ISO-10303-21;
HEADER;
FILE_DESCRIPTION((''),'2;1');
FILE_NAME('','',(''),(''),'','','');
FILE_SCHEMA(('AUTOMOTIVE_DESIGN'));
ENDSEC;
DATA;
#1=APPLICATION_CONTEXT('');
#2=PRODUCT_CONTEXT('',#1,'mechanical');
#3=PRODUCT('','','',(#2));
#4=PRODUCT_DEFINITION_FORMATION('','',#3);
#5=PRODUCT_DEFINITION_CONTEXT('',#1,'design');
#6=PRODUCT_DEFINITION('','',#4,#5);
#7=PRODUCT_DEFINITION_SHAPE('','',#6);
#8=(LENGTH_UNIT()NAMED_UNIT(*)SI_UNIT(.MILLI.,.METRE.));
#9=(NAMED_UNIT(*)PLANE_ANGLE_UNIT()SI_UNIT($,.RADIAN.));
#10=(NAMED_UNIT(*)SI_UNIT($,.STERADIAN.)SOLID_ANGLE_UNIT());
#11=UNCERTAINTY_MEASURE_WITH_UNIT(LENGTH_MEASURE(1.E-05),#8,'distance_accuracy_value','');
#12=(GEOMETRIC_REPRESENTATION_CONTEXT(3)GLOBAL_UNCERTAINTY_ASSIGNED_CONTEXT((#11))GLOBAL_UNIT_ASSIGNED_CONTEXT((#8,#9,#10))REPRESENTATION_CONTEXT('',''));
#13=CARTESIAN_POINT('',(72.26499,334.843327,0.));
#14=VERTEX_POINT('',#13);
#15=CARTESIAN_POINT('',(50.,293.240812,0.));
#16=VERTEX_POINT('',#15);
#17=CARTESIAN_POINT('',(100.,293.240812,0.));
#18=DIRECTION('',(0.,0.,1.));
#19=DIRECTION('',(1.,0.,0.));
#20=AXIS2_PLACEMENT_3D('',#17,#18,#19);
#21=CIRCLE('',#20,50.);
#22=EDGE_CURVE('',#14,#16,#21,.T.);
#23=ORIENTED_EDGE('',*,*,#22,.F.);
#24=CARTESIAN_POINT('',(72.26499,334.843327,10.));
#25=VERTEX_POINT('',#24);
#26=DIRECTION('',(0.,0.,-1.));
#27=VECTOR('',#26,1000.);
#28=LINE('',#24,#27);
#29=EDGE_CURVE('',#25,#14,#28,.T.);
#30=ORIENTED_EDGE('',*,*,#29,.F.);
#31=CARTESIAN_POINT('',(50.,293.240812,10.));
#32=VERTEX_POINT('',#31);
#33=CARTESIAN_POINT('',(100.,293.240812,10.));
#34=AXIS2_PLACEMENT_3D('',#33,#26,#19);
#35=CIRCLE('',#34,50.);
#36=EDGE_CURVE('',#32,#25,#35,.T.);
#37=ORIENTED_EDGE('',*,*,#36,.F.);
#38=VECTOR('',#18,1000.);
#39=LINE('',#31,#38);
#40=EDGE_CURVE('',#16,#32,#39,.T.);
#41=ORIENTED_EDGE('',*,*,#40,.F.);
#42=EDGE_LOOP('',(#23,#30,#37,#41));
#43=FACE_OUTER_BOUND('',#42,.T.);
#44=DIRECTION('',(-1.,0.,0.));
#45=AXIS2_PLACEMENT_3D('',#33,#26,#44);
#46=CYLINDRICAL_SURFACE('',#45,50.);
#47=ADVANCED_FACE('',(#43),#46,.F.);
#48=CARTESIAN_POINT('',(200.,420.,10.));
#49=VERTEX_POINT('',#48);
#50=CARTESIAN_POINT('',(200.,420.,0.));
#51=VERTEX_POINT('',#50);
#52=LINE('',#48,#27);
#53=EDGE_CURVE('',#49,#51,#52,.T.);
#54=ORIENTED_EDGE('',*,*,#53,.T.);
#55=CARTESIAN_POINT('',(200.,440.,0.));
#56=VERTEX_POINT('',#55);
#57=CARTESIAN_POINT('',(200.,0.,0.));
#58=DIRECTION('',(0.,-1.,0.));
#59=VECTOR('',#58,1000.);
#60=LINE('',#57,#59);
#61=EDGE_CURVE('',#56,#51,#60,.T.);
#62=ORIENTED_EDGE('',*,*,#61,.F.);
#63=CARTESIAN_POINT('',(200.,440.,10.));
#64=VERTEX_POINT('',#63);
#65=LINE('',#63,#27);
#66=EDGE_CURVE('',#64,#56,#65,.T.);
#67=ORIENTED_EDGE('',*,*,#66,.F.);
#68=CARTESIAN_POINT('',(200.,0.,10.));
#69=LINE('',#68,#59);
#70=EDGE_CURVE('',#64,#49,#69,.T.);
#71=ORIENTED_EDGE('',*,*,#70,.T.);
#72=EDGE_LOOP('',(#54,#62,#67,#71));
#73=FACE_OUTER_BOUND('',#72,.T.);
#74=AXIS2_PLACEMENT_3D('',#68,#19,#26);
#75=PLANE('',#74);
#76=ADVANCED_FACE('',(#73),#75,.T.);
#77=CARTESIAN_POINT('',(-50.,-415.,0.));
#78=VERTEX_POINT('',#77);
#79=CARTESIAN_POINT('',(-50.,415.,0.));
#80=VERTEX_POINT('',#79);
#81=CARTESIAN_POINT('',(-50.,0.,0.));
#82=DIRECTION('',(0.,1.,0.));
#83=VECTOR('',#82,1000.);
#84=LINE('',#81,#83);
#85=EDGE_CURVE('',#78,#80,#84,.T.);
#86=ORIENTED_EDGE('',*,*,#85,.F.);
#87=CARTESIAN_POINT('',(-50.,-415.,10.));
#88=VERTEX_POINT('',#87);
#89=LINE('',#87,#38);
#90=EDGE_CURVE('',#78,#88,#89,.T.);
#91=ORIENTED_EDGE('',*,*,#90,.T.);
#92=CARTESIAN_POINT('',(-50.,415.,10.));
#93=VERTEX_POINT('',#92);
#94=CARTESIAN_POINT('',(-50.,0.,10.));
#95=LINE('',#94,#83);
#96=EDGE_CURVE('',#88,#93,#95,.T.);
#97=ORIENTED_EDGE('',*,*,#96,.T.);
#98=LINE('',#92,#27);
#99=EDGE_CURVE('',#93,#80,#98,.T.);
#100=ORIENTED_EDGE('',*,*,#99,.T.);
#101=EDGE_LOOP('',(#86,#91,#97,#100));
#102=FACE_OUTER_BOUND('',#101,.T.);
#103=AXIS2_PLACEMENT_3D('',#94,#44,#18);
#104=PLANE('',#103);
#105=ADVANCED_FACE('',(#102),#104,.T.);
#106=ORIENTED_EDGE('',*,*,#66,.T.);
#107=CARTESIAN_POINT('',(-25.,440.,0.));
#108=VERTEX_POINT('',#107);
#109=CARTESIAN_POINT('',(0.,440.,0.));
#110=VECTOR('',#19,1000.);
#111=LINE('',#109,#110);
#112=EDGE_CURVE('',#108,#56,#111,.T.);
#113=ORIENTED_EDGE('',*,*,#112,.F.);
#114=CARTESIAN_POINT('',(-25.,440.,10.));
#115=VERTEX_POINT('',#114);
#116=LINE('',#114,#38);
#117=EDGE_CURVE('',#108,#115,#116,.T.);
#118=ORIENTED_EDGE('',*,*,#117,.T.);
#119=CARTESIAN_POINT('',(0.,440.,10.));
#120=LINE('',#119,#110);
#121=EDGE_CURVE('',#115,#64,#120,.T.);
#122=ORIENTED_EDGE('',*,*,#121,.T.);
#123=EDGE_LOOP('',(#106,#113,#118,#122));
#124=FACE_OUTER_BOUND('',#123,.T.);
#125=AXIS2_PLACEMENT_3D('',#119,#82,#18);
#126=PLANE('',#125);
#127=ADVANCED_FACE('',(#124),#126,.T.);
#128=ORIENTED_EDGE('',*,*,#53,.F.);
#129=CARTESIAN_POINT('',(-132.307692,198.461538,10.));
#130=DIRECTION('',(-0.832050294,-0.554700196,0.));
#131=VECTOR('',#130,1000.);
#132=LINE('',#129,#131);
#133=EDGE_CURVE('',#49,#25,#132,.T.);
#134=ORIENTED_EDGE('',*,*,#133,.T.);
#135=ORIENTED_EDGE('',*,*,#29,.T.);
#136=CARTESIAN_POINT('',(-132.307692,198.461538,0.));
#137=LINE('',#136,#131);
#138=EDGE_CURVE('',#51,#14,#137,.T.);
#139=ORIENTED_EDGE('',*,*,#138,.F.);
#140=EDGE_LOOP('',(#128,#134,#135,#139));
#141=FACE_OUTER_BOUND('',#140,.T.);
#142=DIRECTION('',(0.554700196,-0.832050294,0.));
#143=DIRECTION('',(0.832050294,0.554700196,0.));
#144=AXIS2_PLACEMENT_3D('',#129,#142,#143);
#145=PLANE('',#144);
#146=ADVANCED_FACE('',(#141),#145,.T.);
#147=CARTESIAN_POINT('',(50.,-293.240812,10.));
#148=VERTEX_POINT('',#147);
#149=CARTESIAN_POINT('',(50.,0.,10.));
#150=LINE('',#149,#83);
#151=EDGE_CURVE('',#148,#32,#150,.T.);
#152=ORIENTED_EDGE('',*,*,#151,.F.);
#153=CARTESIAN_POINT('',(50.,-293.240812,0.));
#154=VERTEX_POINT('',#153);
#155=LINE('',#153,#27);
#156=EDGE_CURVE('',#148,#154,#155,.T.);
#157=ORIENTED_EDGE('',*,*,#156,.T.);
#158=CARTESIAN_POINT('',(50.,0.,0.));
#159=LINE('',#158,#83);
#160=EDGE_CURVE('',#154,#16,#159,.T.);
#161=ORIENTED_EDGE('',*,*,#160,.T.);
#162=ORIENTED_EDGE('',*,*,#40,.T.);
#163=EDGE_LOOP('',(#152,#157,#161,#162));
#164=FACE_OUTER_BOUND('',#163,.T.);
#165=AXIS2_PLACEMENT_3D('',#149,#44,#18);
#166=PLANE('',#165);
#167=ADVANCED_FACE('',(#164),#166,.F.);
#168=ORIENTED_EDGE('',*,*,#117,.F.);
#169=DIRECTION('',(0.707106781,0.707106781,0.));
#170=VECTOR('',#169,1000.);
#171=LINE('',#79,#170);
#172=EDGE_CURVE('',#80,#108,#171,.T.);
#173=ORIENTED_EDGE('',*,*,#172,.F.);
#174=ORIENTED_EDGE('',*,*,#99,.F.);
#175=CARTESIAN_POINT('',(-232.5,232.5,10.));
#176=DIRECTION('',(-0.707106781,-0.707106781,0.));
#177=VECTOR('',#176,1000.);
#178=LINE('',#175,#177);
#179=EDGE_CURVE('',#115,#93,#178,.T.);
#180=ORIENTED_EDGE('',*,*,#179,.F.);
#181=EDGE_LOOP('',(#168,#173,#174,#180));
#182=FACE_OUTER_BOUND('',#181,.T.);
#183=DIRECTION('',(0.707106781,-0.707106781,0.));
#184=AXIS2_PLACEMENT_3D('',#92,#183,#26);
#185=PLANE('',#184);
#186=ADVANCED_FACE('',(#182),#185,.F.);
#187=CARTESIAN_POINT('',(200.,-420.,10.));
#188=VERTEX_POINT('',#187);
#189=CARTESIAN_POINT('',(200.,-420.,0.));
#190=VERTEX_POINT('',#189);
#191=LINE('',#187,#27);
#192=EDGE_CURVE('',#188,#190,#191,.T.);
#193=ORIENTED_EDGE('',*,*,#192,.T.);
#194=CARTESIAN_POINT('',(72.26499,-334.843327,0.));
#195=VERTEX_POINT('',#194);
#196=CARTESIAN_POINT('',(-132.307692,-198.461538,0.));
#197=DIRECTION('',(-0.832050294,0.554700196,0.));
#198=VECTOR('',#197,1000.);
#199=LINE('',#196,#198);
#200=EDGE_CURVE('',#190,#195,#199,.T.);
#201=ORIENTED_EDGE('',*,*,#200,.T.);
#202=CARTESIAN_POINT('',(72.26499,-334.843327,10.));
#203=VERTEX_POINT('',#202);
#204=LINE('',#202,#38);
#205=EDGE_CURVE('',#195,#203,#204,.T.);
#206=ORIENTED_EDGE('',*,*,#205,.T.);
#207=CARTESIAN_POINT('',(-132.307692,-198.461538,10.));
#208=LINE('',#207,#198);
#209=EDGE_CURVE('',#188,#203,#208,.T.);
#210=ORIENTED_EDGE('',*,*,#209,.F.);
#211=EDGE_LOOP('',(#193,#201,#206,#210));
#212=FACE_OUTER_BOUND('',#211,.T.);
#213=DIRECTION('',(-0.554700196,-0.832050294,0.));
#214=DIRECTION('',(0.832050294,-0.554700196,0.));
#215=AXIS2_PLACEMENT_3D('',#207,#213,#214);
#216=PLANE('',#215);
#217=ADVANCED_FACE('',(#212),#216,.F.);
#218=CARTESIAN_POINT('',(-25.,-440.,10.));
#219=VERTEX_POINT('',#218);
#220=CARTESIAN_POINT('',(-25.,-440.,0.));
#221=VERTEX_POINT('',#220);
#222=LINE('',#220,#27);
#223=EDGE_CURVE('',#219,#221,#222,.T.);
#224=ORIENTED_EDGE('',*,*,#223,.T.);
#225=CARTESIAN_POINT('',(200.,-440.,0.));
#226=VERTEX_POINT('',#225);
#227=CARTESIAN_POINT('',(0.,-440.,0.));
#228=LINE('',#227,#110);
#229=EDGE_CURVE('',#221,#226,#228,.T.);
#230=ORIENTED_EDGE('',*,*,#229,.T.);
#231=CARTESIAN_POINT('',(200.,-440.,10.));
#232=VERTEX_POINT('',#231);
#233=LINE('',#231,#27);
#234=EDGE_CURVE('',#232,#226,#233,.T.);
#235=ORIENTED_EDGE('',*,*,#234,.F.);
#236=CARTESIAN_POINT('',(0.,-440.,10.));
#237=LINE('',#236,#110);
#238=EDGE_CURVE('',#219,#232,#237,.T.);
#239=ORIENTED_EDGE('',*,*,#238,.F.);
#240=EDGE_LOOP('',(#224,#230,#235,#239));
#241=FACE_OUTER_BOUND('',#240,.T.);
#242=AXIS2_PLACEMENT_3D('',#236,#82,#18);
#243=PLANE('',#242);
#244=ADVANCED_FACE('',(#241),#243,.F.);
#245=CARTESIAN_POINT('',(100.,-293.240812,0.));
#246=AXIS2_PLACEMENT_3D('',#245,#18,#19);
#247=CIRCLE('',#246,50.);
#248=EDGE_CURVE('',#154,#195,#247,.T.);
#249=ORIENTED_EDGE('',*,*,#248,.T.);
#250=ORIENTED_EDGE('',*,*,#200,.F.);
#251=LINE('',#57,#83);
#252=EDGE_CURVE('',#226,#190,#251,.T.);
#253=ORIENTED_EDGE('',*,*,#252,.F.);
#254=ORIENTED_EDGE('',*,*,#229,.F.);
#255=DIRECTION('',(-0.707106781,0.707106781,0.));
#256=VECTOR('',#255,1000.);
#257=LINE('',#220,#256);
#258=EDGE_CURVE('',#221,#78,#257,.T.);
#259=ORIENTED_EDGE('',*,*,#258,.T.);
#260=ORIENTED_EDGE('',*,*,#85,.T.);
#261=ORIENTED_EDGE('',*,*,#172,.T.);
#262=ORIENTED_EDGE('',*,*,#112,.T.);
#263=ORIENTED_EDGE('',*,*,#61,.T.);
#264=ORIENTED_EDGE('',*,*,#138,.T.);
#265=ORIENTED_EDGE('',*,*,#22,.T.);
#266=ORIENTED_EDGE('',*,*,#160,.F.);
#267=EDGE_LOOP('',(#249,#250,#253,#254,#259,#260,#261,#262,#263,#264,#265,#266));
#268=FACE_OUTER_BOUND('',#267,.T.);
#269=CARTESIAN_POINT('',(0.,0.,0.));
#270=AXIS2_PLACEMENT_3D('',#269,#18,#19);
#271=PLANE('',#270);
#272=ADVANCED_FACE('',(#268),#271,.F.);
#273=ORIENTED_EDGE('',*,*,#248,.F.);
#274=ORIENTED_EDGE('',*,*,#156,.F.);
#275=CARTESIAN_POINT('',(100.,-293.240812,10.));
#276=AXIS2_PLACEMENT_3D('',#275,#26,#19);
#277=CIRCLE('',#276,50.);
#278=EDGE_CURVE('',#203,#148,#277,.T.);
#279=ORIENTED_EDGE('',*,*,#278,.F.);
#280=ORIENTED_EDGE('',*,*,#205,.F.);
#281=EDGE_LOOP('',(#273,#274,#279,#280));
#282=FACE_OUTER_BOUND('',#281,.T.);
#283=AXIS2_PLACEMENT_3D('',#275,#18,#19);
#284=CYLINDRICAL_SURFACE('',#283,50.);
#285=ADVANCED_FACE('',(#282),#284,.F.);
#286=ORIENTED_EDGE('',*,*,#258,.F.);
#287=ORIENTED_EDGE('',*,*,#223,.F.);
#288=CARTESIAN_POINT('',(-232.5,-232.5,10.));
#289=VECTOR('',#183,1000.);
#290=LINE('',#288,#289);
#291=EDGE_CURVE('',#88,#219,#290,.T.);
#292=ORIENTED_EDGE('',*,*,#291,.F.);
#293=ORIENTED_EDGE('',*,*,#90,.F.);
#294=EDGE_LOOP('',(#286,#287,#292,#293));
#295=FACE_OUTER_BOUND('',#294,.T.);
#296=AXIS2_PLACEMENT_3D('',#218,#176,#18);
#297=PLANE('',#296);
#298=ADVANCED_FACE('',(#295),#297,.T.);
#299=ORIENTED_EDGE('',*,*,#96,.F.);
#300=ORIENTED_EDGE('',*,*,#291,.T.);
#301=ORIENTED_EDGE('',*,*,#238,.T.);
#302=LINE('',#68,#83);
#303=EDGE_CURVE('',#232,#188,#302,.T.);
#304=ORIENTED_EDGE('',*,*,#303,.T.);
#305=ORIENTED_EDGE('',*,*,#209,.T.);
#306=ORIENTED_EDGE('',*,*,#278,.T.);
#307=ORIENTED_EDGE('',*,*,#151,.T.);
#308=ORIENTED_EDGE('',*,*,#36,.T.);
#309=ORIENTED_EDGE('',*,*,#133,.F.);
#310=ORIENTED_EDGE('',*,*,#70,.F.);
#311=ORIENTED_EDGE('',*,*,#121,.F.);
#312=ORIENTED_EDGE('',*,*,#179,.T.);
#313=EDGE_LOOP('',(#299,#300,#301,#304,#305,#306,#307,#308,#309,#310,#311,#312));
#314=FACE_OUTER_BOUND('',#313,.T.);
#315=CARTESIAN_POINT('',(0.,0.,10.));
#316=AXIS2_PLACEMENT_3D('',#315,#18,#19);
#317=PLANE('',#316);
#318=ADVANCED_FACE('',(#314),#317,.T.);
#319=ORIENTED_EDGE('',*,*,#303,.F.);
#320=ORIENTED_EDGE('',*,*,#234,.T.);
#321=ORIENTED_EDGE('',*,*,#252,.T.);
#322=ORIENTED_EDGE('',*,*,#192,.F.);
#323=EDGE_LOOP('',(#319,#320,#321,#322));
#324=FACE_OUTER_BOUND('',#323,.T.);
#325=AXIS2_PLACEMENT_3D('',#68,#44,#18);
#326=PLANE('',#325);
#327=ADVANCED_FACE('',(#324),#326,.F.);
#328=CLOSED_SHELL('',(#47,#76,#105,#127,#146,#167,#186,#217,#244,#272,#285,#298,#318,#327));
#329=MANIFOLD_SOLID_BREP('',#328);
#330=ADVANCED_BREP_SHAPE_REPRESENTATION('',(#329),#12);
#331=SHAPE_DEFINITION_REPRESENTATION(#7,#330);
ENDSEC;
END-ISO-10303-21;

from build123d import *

# Parameters (mm, degrees)
SKETCH1_W           = 150
SKETCH1_H           = 20
SKETCH1_W_2         = 100
BOSS_EXTRUDE1_DEPTH = 10
FILLET1_R           = 50
CHAMFER1_SIZE       = 25


with BuildPart() as part:
    # Sketch1 → Boss-Extrude1 (new body)
    with BuildSketch(Plane.XY):
        Polygon((200, 420), (50, 420), (50, 320), align=None)
        with Locations((125, 430)):
            Rectangle(SKETCH1_W, SKETCH1_H)
        Polygon((-50, 420), (-50, -420), (50, -420), (50, -320), (50, 320), (50, 420), align=None)
        Polygon((50, -320), (50, -420), (200, -420), align=None)
        with Locations((125, -430)):
            Rectangle(SKETCH1_W, SKETCH1_H)
        with Locations((0, -430)):
            Rectangle(SKETCH1_W_2, SKETCH1_H)
        with Locations((0, 430)):
            Rectangle(SKETCH1_W_2, SKETCH1_H)
    extrude(amount=BOSS_EXTRUDE1_DEPTH)

    # Fillet1
    fillet1_edges = [part.edges().sort_by_distance(p)[0] for p in [
        (50, 320, 5),
        (50, -320, 5),
    ]]
    fillet(fillet1_edges, radius=FILLET1_R)

    # Chamfer1
    chamfer1_edges = [part.edges().sort_by_distance(p)[0] for p in [
        (-50, -440, 5),
        (-50, 440, 5),
    ]]
    chamfer(chamfer1_edges, length=CHAMFER1_SIZE)


solid = part.part
